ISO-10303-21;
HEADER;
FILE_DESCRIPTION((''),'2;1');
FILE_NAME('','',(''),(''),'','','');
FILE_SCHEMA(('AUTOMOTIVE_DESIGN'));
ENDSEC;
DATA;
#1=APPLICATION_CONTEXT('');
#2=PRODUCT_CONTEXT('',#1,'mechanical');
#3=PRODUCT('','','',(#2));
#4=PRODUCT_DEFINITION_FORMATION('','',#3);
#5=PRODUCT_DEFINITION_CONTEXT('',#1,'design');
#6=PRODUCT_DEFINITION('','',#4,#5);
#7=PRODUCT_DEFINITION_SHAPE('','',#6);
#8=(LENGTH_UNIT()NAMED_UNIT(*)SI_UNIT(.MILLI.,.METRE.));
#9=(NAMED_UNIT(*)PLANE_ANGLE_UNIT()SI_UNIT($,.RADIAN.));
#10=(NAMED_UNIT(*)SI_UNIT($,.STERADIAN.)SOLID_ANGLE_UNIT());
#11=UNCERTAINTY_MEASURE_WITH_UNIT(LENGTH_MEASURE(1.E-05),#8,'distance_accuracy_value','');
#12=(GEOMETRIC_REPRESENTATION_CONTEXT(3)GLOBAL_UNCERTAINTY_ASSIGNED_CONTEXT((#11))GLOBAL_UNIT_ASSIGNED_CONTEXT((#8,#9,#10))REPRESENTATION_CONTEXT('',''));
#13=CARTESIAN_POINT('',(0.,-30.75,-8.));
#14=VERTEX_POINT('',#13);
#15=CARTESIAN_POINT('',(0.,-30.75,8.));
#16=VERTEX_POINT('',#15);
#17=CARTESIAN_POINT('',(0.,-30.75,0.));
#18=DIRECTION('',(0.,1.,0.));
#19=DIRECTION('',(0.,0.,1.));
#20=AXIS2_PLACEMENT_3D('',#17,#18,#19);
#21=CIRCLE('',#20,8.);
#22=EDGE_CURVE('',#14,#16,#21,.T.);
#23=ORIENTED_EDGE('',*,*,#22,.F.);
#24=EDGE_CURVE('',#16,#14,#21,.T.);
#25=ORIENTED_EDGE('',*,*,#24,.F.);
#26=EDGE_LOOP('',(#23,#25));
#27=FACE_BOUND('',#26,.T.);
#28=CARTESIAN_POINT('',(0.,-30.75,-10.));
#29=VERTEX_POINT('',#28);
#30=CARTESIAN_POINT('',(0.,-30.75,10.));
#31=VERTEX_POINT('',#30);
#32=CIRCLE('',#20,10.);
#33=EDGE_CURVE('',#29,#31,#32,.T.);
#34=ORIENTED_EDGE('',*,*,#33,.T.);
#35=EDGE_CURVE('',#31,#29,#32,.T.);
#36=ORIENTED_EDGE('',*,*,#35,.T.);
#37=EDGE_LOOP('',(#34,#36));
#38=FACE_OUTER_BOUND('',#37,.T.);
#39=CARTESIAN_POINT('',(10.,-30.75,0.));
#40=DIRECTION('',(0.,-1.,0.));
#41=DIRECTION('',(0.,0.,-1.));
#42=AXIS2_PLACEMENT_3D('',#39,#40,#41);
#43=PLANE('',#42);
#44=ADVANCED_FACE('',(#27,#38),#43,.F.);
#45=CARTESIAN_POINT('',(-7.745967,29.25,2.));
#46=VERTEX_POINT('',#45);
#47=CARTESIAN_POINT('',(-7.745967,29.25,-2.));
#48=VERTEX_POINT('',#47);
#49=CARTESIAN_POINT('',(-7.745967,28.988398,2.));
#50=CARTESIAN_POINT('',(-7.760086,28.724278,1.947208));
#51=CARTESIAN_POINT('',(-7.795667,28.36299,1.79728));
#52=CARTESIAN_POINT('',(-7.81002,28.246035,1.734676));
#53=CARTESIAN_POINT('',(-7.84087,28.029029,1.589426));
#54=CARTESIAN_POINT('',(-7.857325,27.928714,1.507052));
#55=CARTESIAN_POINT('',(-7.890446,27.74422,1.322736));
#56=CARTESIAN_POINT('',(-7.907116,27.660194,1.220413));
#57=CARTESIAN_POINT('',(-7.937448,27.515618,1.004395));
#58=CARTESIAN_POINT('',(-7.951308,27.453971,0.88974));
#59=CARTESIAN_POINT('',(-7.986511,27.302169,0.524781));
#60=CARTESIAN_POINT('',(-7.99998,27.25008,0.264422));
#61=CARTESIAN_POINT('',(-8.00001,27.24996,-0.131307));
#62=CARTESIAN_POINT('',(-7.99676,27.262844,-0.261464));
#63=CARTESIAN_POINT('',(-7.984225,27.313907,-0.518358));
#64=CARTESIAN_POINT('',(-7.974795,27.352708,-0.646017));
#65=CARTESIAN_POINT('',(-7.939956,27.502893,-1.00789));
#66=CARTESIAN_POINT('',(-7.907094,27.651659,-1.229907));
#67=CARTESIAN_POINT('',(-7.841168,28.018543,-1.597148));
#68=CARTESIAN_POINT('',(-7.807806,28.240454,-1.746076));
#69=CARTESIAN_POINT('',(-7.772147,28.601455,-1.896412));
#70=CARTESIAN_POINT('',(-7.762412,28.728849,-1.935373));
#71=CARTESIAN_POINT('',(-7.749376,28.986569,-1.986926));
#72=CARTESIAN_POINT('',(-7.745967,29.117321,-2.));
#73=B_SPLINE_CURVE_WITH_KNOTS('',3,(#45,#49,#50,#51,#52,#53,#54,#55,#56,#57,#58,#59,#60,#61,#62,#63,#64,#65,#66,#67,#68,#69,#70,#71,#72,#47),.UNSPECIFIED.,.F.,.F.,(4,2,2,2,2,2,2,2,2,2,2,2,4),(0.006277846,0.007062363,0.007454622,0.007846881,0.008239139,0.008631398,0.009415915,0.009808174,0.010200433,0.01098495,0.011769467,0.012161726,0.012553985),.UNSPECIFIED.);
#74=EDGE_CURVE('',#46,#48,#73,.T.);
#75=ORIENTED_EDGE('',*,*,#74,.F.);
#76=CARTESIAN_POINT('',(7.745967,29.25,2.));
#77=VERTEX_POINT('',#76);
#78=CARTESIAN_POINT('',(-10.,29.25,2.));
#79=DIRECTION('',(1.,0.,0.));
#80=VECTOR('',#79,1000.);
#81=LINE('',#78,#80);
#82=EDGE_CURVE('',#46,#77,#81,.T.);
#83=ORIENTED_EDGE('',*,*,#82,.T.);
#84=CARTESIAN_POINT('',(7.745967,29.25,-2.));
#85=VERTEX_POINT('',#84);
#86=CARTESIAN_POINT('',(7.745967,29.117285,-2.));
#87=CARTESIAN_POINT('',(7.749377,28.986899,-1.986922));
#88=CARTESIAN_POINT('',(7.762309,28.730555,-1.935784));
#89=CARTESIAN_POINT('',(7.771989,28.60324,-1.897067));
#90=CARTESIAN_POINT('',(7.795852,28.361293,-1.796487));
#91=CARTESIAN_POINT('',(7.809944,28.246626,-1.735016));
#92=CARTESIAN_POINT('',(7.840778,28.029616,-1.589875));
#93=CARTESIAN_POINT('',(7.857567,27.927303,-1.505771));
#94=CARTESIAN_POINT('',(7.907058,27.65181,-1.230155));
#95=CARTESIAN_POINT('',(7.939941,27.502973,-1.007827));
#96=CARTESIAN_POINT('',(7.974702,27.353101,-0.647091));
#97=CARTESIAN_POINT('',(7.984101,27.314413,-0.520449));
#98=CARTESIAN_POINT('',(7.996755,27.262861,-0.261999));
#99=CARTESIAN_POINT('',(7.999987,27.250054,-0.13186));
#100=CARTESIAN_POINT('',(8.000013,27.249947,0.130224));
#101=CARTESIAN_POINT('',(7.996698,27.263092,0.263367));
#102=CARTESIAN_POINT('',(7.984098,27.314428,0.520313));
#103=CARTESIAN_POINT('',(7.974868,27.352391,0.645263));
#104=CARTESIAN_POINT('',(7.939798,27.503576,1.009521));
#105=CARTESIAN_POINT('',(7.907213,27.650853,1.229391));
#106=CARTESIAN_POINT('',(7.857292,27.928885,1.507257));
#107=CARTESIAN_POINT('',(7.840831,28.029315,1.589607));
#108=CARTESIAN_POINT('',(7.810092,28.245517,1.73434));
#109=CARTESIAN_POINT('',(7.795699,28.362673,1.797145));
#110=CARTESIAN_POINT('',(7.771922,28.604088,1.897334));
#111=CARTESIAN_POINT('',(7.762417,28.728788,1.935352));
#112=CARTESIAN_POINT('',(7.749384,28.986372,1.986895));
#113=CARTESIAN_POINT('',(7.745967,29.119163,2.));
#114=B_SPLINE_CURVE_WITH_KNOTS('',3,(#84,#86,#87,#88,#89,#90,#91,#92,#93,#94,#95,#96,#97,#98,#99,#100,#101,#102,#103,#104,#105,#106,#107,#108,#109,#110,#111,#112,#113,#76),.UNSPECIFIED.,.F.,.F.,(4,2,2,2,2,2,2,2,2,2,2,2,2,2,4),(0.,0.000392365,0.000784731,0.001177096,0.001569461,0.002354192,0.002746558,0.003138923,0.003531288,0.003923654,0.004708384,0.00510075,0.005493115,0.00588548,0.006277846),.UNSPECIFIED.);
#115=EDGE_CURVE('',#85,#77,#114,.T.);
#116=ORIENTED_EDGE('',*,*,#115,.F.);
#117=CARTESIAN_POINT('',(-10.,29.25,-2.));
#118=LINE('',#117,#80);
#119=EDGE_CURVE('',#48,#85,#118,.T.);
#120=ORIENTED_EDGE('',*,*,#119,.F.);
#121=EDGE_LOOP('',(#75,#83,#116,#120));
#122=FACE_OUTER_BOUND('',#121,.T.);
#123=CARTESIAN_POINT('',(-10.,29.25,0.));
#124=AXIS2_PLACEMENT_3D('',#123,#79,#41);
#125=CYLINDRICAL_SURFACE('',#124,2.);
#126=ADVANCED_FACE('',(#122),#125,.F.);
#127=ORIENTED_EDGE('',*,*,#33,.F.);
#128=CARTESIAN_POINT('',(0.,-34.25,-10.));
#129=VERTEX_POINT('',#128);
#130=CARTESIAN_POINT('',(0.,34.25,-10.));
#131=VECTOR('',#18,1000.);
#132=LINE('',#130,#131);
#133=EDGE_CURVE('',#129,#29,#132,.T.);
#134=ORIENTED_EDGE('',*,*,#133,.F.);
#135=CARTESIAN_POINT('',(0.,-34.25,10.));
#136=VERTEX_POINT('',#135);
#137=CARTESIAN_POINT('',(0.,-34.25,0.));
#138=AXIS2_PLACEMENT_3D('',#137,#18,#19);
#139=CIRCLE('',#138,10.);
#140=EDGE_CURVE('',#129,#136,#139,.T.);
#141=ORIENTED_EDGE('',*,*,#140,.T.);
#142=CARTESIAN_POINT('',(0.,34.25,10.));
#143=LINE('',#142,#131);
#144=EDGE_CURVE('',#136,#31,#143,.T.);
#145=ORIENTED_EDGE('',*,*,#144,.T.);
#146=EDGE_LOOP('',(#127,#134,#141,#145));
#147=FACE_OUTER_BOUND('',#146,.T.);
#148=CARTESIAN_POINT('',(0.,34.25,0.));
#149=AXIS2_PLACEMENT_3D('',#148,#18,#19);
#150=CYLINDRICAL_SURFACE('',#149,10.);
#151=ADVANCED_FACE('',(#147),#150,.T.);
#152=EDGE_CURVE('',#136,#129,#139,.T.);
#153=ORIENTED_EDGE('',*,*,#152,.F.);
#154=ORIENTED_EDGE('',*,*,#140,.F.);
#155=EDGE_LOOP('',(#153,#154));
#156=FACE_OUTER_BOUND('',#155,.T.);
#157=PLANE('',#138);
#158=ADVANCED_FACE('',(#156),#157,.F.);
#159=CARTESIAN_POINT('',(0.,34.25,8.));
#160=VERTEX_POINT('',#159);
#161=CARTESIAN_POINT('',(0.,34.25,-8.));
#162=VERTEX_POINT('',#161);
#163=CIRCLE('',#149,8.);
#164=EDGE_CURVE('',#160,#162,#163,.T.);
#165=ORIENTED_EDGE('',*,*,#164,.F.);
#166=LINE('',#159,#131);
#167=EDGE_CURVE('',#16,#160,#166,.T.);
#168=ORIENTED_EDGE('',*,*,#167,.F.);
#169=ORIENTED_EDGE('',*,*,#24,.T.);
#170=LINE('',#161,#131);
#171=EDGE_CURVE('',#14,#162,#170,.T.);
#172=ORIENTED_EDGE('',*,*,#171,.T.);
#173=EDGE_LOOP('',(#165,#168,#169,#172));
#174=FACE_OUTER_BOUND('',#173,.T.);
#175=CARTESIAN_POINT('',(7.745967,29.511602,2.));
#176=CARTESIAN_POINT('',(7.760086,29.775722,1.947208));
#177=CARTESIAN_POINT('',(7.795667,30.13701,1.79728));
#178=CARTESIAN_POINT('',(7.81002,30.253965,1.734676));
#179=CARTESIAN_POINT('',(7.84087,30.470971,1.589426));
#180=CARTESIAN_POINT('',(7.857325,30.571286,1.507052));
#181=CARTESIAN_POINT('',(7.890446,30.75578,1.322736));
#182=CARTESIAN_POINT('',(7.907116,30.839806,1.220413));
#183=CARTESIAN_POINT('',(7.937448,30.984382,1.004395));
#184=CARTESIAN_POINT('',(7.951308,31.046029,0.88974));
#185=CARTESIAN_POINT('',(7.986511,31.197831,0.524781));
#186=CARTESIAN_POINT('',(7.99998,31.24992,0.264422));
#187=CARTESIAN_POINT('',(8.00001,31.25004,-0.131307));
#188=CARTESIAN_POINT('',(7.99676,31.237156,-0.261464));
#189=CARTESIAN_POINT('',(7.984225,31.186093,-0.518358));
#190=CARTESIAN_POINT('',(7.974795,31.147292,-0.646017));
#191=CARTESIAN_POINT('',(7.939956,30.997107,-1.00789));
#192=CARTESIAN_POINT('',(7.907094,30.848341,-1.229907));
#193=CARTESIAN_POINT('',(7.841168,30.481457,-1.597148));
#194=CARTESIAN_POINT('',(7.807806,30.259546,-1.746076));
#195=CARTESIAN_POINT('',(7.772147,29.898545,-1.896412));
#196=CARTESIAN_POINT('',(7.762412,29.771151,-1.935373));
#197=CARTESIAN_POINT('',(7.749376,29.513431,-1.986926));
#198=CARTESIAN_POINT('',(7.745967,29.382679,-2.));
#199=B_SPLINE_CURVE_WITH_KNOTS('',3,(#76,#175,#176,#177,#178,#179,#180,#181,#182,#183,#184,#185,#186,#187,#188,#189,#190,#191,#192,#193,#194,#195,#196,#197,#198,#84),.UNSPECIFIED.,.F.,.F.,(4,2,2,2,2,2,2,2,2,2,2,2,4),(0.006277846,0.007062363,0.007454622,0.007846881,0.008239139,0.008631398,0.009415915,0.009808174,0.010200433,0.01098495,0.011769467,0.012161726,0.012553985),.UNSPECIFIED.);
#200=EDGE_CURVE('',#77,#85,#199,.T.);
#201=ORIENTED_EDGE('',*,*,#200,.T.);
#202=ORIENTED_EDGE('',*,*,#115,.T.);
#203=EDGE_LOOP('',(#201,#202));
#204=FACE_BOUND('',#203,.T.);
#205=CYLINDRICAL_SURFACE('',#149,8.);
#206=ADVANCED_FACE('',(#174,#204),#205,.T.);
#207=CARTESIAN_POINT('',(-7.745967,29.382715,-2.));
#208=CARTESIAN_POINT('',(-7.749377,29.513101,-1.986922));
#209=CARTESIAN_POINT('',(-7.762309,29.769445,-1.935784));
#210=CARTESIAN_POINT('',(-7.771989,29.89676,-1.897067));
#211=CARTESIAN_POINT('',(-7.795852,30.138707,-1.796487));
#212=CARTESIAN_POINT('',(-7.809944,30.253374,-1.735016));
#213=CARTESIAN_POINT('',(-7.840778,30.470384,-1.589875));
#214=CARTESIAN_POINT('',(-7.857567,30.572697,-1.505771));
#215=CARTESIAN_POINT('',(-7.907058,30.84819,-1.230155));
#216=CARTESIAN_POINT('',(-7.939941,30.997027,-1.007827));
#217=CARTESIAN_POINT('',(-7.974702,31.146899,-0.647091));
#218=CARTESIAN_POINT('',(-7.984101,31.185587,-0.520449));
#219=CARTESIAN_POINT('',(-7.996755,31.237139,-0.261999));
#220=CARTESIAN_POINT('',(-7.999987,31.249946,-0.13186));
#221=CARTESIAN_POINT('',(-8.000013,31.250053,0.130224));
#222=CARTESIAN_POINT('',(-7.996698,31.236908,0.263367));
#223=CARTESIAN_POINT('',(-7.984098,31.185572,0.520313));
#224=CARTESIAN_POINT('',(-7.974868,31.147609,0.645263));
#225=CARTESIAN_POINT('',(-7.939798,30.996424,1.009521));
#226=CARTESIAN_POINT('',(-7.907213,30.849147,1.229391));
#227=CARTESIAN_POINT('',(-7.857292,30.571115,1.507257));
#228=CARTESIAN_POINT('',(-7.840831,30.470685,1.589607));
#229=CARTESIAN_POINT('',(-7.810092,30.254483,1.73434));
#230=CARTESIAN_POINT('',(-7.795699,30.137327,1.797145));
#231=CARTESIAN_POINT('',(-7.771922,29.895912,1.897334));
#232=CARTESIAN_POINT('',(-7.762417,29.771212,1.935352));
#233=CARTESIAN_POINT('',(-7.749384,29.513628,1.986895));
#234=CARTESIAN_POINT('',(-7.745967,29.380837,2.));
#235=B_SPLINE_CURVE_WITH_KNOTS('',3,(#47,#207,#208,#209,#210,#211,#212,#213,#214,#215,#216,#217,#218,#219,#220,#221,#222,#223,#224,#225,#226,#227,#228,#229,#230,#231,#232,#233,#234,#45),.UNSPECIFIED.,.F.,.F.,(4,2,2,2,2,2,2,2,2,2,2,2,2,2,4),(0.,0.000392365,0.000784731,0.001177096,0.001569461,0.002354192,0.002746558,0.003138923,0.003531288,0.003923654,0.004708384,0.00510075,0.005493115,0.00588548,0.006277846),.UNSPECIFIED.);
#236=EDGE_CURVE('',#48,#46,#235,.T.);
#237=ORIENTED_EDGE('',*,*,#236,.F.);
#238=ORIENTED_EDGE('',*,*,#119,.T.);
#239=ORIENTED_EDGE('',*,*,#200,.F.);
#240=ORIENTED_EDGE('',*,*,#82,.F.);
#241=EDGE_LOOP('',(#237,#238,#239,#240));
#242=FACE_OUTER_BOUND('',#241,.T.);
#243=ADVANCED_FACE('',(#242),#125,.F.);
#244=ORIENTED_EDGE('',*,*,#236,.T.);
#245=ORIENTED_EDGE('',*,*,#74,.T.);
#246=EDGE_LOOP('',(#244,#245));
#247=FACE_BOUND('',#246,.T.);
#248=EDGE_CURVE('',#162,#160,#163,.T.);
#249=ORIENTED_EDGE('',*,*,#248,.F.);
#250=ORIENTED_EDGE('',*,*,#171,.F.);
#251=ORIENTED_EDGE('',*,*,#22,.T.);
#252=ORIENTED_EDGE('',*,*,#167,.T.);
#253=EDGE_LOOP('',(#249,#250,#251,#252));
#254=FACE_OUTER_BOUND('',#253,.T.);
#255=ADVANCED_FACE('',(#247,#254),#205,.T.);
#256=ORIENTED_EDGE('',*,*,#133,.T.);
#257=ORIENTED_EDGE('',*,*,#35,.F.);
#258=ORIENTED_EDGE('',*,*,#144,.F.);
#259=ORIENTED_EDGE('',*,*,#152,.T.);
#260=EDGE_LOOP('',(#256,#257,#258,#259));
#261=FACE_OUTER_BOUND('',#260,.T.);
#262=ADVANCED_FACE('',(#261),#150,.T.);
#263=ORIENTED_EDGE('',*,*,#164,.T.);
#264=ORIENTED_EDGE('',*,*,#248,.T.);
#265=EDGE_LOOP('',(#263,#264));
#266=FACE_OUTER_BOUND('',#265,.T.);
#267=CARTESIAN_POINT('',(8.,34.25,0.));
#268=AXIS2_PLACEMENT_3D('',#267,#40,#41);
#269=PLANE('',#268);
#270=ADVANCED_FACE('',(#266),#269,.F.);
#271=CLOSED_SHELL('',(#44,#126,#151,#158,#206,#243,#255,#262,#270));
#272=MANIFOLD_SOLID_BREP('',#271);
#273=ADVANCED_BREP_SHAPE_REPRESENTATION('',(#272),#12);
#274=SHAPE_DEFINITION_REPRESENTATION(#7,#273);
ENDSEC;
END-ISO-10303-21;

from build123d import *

# Parameters (mm, degrees)
SKETCH_2_R          = 2
CUT_EXTRUDE_1_DEPTH = 10


with BuildPart() as part:
    # 草图1 → 旋转1 (revolve)
    with BuildSketch(Plane.XY, mode=Mode.PRIVATE) as revolve_1_sk:
        Polygon((0, 34.25), (0, -34.25), (10, -34.25), (10, -30.75), (8, -30.75), (8, 34.25), align=None)
    revolve(revolve_1_sk.sketch.rotate(Axis((0, 34.25, 0), (0, -1, 0)), 90), axis=Axis((0, 34.25, 0), (0, -1, 0)))

    # 草图2 → 切除-拉伸1 (cut, symmetric)
    with BuildSketch(Plane(origin=(0, 0, 0), x_dir=(0, 0, -1), z_dir=(1, 0, 0))):
        with Locations((0, 29.25)):
            Circle(SKETCH_2_R)
    extrude(amount=CUT_EXTRUDE_1_DEPTH, both=True, mode=Mode.SUBTRACT)


solid = part.part
